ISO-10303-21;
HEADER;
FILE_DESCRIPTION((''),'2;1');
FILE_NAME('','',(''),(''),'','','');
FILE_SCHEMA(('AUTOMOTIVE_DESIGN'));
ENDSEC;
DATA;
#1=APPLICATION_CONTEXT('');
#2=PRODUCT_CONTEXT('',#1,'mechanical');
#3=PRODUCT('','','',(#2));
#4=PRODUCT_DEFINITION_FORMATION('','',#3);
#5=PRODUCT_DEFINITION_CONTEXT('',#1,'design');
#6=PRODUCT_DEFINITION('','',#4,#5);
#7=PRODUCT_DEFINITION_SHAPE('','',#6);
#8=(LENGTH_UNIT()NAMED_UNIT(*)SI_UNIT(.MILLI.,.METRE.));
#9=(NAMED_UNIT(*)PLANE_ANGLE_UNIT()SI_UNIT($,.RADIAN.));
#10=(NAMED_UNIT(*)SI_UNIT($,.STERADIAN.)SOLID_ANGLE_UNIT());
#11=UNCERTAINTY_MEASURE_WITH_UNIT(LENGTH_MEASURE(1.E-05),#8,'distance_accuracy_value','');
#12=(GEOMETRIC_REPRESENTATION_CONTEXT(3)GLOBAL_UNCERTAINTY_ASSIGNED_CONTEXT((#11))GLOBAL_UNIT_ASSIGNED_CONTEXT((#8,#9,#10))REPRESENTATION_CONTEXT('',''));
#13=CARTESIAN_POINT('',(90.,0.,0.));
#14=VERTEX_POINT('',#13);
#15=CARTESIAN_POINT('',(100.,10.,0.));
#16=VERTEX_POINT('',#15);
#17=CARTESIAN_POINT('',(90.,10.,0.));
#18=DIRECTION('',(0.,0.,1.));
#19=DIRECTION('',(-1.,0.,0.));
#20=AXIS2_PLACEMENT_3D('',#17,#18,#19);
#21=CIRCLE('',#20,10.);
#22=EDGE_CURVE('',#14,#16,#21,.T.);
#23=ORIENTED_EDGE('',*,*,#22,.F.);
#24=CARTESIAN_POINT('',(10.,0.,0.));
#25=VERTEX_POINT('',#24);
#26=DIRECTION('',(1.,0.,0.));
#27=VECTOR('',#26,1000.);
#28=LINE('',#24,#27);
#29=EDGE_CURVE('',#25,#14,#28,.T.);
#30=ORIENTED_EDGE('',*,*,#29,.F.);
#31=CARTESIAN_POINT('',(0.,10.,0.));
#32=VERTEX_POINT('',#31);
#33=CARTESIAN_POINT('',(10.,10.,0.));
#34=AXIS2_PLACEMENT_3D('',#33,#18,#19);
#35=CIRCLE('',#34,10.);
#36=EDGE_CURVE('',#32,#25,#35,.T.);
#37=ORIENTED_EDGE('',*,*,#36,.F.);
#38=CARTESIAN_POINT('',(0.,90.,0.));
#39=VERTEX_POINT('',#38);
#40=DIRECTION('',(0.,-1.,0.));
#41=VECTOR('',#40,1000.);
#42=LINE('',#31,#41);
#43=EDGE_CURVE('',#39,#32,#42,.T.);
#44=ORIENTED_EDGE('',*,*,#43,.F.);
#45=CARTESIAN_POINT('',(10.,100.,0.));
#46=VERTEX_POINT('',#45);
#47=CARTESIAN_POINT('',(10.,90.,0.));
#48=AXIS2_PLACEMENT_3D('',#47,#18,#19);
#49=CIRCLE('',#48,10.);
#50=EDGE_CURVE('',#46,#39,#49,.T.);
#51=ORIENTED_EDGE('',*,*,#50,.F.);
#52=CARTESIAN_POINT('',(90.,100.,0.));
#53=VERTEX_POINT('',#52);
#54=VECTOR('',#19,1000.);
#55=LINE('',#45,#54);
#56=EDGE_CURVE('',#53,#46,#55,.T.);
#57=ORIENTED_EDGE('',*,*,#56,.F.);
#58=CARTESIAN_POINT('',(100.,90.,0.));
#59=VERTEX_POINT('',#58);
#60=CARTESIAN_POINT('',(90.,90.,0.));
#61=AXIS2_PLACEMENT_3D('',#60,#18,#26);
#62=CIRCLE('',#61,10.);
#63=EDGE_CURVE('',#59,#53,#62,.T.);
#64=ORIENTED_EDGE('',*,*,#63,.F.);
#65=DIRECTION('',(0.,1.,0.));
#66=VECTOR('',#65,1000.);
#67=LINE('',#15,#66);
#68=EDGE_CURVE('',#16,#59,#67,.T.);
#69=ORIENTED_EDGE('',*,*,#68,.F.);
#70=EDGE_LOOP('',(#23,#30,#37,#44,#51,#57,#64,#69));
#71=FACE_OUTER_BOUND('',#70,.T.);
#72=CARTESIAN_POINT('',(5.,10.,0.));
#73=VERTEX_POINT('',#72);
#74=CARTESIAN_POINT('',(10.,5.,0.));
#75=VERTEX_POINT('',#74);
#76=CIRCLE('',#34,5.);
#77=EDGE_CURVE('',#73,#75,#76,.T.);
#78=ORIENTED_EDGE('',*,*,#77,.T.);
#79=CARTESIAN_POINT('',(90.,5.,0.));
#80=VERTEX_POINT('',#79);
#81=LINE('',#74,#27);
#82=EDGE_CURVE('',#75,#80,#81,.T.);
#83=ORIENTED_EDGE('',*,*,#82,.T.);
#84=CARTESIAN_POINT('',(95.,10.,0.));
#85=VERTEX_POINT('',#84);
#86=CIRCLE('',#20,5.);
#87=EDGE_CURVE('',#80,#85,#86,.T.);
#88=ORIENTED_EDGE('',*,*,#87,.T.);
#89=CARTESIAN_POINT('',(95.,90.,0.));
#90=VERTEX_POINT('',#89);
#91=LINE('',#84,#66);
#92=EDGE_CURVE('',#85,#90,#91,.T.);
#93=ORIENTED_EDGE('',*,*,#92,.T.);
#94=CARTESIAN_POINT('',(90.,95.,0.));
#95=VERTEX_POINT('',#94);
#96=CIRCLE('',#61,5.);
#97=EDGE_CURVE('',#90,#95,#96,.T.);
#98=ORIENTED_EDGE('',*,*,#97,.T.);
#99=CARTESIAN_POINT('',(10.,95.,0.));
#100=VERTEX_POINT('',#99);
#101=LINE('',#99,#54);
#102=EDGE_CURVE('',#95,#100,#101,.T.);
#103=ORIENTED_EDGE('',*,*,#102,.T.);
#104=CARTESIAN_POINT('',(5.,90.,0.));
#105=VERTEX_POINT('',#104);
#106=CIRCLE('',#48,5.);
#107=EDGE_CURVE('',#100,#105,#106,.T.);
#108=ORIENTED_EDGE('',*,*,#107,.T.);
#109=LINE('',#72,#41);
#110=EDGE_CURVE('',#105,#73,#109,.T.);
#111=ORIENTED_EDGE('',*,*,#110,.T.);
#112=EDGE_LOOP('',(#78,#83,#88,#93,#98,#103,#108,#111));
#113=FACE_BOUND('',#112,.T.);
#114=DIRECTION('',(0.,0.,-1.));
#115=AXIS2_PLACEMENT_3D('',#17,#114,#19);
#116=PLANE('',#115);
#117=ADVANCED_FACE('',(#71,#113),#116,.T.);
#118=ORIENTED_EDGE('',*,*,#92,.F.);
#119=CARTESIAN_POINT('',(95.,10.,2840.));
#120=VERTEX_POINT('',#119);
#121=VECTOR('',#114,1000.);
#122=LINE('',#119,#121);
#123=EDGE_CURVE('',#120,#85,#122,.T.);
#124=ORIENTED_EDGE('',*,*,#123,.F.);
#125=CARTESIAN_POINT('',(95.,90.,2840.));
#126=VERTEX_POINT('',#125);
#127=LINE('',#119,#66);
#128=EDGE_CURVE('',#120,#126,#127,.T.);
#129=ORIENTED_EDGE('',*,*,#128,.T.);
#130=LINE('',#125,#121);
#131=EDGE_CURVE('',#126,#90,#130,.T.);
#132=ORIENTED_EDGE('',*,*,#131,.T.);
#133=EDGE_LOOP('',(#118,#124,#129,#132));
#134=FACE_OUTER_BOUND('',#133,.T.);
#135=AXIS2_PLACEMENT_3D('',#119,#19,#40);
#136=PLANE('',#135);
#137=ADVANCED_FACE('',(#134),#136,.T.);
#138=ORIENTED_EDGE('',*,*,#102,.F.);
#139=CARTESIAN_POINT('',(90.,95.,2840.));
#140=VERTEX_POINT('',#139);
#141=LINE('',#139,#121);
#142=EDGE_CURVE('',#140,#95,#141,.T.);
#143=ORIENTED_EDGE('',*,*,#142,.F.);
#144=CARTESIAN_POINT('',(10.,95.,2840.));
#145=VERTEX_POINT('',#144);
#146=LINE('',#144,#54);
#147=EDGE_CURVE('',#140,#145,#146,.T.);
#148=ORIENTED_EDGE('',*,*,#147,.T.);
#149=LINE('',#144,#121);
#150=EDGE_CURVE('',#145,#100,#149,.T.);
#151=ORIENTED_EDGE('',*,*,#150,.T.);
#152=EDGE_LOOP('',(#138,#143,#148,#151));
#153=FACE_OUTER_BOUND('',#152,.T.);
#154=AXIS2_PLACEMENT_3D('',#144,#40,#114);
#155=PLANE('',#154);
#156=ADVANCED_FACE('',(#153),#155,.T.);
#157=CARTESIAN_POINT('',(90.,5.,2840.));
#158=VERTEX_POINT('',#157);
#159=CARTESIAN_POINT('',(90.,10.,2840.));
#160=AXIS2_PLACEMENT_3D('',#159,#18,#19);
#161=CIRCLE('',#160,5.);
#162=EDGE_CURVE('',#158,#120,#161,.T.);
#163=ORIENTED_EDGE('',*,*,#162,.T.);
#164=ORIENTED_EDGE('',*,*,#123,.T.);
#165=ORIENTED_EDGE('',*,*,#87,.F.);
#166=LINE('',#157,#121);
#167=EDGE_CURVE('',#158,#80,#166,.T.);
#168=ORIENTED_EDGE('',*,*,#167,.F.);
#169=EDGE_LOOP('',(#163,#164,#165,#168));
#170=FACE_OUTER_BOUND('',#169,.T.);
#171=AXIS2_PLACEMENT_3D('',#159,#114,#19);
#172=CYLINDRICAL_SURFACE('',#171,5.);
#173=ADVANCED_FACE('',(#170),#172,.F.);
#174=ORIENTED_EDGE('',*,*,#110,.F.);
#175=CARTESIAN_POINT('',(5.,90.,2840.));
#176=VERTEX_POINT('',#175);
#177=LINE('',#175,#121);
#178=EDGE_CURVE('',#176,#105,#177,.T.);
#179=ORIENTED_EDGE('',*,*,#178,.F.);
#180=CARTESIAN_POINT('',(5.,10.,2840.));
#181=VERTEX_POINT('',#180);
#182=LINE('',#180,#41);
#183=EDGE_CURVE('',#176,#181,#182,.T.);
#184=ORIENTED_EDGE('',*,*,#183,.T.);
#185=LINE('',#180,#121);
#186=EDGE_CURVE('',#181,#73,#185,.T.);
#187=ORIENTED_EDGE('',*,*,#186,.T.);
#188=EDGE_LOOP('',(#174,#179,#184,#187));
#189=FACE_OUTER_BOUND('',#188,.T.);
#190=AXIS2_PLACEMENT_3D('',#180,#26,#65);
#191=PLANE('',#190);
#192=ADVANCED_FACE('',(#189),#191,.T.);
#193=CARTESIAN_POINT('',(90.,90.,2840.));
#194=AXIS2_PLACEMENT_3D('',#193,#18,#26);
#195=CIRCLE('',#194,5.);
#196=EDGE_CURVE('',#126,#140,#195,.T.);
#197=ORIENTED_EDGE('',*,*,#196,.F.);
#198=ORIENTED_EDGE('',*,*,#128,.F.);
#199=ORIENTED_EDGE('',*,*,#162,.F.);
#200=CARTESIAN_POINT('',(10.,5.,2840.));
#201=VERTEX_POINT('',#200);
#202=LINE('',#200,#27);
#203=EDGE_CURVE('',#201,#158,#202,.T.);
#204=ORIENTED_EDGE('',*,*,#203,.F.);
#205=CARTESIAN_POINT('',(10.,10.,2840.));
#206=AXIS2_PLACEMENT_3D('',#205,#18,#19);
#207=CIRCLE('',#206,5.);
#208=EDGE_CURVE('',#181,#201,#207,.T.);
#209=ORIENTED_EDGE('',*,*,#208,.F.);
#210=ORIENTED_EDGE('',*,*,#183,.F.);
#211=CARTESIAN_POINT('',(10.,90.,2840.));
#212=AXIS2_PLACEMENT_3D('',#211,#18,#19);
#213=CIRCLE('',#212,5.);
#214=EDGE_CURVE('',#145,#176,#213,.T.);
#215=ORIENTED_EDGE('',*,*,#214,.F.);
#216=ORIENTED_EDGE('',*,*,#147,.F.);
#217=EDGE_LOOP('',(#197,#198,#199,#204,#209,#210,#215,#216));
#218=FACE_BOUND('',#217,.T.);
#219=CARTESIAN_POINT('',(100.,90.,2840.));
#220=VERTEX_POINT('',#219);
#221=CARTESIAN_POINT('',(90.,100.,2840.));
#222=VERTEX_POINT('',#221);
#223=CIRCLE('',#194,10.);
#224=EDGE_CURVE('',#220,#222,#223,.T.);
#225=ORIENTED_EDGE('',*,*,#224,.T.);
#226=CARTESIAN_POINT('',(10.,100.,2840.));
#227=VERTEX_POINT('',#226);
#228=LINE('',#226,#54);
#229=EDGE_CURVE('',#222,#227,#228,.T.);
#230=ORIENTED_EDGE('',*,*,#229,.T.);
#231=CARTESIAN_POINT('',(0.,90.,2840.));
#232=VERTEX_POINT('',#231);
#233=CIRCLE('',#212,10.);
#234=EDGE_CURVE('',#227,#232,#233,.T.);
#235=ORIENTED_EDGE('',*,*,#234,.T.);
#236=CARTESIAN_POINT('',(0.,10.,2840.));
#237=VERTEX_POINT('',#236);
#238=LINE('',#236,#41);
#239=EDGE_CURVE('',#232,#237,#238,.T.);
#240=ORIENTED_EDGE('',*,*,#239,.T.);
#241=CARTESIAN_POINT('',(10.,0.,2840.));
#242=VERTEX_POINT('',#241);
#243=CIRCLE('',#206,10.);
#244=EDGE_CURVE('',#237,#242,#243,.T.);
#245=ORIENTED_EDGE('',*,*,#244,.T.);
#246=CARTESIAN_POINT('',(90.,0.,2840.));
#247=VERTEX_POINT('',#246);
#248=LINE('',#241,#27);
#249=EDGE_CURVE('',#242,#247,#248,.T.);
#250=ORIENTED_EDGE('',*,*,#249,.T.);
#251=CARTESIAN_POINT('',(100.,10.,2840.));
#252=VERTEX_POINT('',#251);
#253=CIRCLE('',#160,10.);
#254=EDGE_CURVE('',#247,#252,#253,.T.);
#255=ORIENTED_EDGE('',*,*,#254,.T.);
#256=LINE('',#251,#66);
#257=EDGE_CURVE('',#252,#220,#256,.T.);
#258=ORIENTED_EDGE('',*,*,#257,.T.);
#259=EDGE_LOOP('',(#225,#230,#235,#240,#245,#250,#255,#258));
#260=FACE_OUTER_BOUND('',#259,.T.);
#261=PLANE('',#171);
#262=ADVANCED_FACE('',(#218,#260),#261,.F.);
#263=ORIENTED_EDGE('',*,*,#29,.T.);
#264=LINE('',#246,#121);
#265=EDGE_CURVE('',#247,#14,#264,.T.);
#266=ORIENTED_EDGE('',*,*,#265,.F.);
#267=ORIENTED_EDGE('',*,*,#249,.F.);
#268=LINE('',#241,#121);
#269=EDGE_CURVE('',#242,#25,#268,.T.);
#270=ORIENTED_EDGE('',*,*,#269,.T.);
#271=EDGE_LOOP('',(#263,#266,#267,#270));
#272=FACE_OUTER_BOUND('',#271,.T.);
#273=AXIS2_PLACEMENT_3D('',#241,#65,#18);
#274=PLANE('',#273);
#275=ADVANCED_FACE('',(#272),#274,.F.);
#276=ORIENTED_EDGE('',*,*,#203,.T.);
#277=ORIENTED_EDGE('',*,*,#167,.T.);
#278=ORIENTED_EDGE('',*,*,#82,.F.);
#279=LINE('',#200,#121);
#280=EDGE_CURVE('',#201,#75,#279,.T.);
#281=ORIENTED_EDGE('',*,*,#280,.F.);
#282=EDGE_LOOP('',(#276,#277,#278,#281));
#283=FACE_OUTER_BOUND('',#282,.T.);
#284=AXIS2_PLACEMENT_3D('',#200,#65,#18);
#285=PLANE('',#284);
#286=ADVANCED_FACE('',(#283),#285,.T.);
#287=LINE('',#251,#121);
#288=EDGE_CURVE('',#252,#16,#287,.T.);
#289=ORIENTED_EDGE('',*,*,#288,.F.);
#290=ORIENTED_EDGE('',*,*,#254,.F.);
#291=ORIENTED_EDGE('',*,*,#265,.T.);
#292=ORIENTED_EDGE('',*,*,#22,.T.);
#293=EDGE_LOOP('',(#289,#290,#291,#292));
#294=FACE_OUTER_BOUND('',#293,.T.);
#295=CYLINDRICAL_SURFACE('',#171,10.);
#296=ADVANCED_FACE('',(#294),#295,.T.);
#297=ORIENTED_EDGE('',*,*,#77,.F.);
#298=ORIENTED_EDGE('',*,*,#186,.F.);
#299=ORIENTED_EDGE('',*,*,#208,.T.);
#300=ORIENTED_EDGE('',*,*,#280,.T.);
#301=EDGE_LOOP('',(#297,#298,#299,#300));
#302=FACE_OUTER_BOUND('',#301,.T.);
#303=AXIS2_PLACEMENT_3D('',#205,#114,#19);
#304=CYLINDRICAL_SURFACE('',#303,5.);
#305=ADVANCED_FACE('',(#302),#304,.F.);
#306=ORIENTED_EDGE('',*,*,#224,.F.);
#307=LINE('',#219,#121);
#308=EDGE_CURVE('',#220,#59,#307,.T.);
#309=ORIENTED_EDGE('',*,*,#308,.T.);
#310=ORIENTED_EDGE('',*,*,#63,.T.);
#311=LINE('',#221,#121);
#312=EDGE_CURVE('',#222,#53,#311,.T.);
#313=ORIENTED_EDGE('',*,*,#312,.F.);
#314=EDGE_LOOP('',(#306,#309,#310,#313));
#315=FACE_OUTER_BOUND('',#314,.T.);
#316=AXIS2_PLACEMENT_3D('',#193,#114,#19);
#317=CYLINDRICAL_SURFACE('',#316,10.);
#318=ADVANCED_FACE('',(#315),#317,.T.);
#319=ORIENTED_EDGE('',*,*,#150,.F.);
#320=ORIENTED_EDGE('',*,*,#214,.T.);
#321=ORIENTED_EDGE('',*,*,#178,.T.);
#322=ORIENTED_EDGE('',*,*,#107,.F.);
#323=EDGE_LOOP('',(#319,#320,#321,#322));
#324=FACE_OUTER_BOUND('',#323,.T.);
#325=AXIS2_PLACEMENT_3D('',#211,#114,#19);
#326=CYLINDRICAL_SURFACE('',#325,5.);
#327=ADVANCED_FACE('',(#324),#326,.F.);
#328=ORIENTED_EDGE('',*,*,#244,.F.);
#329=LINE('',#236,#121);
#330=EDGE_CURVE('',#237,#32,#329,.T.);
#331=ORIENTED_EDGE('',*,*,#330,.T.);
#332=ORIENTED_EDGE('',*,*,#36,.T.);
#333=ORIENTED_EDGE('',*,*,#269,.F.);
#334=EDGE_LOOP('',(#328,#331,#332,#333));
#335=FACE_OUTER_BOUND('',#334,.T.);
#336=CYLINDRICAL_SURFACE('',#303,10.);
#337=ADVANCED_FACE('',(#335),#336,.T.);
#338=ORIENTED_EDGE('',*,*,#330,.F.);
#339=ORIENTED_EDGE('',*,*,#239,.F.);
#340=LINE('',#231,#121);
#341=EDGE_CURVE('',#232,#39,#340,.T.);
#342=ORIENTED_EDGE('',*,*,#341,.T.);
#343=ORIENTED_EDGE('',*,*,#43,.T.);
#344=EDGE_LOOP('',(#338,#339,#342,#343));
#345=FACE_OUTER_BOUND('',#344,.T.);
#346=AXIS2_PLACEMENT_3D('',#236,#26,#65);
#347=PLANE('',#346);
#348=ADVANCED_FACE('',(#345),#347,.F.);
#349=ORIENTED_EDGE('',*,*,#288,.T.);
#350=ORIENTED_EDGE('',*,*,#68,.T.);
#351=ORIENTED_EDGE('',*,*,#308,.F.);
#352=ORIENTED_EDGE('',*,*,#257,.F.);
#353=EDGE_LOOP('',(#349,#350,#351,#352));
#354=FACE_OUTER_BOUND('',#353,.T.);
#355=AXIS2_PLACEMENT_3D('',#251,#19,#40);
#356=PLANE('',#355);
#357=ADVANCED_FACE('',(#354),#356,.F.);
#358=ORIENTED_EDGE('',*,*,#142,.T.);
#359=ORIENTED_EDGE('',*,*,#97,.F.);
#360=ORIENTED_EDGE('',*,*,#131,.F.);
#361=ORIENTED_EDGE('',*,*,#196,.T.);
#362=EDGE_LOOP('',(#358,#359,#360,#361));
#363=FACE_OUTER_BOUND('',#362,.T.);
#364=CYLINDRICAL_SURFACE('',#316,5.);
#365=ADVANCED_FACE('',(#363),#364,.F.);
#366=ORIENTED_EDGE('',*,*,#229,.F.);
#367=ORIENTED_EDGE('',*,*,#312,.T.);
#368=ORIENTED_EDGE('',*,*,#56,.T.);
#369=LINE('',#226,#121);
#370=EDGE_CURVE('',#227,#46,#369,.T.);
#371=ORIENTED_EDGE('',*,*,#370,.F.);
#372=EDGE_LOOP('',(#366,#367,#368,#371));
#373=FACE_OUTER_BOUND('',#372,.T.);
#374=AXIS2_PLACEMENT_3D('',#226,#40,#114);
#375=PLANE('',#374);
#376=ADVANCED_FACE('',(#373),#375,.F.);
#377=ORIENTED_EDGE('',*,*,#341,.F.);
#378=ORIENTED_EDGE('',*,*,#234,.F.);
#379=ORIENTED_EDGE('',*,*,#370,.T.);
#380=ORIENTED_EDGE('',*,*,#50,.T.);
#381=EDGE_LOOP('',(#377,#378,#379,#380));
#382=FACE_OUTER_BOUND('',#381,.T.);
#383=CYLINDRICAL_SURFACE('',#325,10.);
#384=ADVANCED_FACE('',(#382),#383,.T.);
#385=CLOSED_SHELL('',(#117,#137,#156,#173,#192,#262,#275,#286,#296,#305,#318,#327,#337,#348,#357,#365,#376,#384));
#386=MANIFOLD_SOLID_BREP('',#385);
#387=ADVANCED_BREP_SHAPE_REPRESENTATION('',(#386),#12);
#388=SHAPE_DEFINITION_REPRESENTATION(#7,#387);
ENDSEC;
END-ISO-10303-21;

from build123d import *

# Parameters (mm, degrees)
BOSS_EXTRUDE1_DEPTH = 2840


with BuildPart() as part:
    # Sketch1 → Boss-Extrude1 (new body)
    with BuildSketch(Plane.XY):
        with BuildLine():
            Line((10, 0), (90, 0))
            ThreePointArc((90, 0), (97.071067812, 2.928932188), (100, 10))
            Line((100, 10), (100, 90))
            ThreePointArc((100, 90), (97.071067812, 97.071067812), (90, 100))
            Line((90, 100), (10, 100))
            ThreePointArc((10, 100), (2.928932188, 97.071067812), (0, 90))
            Line((0, 90), (0, 10))
            ThreePointArc((0, 10), (2.928932188, 2.928932188), (10, 0))
        make_face()
        with BuildLine():
            Line((10, 95), (90, 95))
            ThreePointArc((90, 95), (93.535533906, 93.535533906), (95, 90))
            Line((95, 90), (95, 10))
            ThreePointArc((95, 10), (93.535533906, 6.464466094), (90, 5))
            Line((90, 5), (10, 5))
            ThreePointArc((10, 5), (6.464466094, 6.464466094), (5, 10))
            Line((5, 10), (5, 90))
            ThreePointArc((5, 90), (6.464466094, 93.535533906), (10, 95))
        make_face(mode=Mode.SUBTRACT)
    extrude(amount=BOSS_EXTRUDE1_DEPTH)


solid = part.part
